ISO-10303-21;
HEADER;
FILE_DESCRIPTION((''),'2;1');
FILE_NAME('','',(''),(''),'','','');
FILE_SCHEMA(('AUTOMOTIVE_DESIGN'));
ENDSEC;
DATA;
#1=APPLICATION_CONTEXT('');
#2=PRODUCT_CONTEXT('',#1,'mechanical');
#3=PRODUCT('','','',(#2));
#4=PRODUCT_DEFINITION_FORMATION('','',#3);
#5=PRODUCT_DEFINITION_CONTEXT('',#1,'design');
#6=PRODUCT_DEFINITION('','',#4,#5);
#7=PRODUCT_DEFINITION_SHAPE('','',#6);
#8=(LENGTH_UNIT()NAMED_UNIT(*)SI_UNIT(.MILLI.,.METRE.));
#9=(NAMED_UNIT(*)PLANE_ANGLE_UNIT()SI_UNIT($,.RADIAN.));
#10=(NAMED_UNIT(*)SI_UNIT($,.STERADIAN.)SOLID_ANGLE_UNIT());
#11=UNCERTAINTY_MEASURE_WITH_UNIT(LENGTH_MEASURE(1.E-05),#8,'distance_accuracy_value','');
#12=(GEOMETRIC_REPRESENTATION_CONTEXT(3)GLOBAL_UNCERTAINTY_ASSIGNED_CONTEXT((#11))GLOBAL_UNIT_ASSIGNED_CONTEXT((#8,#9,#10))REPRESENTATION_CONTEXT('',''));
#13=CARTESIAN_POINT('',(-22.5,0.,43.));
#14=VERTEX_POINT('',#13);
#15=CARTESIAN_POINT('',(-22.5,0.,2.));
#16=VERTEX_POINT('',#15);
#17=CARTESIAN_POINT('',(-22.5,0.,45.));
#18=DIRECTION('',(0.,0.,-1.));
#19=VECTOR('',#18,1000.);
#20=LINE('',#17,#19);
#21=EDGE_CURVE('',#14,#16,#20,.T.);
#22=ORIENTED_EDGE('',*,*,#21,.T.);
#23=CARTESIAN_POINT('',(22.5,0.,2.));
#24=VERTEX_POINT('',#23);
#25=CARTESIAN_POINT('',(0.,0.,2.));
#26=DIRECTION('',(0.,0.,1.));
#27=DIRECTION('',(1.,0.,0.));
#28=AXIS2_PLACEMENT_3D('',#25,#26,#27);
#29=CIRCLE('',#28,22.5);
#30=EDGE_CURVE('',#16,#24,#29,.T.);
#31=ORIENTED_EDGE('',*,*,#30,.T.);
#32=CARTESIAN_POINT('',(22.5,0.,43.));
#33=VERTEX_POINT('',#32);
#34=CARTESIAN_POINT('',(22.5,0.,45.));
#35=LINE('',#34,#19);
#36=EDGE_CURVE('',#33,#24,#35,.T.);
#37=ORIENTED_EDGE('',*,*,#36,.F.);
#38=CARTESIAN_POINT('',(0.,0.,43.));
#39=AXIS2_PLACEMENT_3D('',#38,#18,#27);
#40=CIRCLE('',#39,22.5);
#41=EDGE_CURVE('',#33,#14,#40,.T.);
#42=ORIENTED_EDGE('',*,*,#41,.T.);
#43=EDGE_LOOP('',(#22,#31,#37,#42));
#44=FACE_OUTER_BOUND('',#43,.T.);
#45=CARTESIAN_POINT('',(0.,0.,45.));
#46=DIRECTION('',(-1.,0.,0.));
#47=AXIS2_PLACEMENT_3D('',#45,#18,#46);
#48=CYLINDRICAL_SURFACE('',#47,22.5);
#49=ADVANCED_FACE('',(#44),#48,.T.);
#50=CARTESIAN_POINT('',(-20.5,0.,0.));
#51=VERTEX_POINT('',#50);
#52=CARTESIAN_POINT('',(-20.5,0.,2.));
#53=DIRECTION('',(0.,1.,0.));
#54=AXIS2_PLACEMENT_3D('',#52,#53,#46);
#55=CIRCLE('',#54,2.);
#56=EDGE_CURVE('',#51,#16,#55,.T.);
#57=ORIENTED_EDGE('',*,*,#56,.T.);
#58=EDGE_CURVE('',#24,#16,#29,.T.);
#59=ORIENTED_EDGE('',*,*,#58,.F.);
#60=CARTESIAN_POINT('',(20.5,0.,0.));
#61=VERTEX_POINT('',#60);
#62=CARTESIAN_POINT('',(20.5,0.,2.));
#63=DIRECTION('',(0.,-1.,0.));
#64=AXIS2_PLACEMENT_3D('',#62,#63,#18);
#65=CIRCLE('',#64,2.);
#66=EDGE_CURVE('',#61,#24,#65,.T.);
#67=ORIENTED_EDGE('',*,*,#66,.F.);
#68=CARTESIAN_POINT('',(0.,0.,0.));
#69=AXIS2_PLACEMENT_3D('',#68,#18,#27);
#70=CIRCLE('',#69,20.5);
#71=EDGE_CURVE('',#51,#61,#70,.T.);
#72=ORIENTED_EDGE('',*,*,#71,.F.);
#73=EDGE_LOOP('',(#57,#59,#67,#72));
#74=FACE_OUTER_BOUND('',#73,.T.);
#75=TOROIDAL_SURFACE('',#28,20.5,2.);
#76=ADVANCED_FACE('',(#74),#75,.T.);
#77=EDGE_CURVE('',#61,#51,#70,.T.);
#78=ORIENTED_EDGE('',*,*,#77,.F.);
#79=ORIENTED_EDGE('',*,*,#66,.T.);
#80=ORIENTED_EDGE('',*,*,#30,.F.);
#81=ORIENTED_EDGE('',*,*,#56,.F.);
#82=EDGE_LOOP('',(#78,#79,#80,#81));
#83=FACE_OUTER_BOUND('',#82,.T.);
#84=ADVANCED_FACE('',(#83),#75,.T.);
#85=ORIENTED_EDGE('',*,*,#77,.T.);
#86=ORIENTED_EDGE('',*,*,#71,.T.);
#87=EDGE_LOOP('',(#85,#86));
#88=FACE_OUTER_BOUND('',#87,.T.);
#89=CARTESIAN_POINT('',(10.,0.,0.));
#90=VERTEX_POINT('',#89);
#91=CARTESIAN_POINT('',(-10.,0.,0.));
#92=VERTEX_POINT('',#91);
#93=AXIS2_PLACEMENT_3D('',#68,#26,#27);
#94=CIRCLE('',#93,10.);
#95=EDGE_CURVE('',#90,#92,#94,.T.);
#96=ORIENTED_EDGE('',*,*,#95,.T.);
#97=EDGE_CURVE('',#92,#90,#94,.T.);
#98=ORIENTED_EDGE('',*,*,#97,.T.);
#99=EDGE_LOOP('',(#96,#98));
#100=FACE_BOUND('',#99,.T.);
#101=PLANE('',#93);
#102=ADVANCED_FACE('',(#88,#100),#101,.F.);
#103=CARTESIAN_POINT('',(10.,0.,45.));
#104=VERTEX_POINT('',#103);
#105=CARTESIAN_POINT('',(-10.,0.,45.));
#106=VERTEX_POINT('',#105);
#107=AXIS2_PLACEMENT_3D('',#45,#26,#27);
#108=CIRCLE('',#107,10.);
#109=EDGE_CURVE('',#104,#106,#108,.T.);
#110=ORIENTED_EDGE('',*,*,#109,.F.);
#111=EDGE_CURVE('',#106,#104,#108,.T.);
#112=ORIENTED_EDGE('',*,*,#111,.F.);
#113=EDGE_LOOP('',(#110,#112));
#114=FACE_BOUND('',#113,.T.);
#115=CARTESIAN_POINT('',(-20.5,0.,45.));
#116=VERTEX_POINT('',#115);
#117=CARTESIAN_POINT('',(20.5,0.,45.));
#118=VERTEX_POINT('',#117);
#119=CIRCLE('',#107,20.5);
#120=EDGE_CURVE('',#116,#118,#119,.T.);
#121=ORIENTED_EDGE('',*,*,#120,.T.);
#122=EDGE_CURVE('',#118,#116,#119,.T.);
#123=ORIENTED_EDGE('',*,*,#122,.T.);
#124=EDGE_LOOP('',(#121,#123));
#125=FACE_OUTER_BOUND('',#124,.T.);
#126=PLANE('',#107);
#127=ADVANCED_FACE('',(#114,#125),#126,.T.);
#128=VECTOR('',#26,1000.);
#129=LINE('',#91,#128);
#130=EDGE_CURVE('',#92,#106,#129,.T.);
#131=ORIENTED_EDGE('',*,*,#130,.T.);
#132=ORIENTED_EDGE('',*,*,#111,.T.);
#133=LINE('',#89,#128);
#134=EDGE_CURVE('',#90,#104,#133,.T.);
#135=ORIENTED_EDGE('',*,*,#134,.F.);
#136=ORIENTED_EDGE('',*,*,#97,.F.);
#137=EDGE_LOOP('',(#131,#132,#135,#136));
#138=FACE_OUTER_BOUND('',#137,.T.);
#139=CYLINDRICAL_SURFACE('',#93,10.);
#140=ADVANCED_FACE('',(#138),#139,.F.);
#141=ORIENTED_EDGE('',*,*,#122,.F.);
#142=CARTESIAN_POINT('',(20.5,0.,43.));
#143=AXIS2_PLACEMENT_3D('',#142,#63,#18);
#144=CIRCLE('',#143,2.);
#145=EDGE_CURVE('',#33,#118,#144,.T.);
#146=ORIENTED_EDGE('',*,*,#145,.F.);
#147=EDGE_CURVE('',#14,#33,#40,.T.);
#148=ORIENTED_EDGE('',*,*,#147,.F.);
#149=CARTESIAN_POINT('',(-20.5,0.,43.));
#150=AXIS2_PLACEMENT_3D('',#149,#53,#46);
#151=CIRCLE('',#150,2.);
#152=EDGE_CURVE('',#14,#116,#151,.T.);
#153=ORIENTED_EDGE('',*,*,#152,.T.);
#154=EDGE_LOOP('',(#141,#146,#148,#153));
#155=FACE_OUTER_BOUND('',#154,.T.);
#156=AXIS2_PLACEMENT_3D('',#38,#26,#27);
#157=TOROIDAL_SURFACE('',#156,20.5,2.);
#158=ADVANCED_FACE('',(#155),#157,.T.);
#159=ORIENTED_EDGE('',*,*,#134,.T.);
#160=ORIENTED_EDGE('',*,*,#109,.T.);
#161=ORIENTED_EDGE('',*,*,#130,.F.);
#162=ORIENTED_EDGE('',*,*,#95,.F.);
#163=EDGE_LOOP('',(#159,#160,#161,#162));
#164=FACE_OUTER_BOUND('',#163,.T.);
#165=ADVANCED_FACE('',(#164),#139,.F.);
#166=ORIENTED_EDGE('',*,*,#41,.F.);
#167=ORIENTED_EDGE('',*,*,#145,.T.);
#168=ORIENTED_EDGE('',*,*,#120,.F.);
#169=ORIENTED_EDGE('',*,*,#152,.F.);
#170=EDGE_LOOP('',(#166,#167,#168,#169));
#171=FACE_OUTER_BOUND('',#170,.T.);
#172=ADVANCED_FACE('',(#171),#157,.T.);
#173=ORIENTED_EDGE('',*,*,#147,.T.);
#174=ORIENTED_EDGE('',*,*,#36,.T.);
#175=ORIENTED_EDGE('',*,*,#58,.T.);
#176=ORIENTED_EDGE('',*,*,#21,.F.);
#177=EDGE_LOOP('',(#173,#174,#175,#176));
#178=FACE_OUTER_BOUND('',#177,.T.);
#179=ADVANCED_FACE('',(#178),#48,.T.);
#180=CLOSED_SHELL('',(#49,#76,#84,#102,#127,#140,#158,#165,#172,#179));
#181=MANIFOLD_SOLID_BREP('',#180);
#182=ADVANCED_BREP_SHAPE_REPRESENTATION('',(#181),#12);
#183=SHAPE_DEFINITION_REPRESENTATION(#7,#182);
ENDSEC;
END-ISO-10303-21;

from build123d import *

# Parameters (mm, degrees)
SKETCH_1_R          = 22.5
EXTRUDE_1_DEPTH     = 45
FILLET_1_R          = 2
SKETCH_2_R          = 10
CUT_EXTRUDE_1_DEPTH = 56.113519253


with BuildPart() as part:
    # 草图1 → 凸台-拉伸1 (new body)
    with BuildSketch(Plane.XY):
        with Locations(Location((0, 0, 0), (0, 0, 180))):
            Circle(SKETCH_1_R)
    extrude(amount=EXTRUDE_1_DEPTH)

    # 圆角1
    fillet_1_edges = [part.edges().sort_by_distance(p)[0] for p in [
        (22.5, 0, 0),
        (22.5, 0, 45),
    ]]
    fillet(fillet_1_edges, radius=FILLET_1_R)

    # 草图2 → 切除-拉伸1 (cut, through all)
    with BuildSketch(Plane.XY.offset(45)):
        Circle(SKETCH_2_R)
    extrude(amount=-CUT_EXTRUDE_1_DEPTH, mode=Mode.SUBTRACT)


solid = part.part
